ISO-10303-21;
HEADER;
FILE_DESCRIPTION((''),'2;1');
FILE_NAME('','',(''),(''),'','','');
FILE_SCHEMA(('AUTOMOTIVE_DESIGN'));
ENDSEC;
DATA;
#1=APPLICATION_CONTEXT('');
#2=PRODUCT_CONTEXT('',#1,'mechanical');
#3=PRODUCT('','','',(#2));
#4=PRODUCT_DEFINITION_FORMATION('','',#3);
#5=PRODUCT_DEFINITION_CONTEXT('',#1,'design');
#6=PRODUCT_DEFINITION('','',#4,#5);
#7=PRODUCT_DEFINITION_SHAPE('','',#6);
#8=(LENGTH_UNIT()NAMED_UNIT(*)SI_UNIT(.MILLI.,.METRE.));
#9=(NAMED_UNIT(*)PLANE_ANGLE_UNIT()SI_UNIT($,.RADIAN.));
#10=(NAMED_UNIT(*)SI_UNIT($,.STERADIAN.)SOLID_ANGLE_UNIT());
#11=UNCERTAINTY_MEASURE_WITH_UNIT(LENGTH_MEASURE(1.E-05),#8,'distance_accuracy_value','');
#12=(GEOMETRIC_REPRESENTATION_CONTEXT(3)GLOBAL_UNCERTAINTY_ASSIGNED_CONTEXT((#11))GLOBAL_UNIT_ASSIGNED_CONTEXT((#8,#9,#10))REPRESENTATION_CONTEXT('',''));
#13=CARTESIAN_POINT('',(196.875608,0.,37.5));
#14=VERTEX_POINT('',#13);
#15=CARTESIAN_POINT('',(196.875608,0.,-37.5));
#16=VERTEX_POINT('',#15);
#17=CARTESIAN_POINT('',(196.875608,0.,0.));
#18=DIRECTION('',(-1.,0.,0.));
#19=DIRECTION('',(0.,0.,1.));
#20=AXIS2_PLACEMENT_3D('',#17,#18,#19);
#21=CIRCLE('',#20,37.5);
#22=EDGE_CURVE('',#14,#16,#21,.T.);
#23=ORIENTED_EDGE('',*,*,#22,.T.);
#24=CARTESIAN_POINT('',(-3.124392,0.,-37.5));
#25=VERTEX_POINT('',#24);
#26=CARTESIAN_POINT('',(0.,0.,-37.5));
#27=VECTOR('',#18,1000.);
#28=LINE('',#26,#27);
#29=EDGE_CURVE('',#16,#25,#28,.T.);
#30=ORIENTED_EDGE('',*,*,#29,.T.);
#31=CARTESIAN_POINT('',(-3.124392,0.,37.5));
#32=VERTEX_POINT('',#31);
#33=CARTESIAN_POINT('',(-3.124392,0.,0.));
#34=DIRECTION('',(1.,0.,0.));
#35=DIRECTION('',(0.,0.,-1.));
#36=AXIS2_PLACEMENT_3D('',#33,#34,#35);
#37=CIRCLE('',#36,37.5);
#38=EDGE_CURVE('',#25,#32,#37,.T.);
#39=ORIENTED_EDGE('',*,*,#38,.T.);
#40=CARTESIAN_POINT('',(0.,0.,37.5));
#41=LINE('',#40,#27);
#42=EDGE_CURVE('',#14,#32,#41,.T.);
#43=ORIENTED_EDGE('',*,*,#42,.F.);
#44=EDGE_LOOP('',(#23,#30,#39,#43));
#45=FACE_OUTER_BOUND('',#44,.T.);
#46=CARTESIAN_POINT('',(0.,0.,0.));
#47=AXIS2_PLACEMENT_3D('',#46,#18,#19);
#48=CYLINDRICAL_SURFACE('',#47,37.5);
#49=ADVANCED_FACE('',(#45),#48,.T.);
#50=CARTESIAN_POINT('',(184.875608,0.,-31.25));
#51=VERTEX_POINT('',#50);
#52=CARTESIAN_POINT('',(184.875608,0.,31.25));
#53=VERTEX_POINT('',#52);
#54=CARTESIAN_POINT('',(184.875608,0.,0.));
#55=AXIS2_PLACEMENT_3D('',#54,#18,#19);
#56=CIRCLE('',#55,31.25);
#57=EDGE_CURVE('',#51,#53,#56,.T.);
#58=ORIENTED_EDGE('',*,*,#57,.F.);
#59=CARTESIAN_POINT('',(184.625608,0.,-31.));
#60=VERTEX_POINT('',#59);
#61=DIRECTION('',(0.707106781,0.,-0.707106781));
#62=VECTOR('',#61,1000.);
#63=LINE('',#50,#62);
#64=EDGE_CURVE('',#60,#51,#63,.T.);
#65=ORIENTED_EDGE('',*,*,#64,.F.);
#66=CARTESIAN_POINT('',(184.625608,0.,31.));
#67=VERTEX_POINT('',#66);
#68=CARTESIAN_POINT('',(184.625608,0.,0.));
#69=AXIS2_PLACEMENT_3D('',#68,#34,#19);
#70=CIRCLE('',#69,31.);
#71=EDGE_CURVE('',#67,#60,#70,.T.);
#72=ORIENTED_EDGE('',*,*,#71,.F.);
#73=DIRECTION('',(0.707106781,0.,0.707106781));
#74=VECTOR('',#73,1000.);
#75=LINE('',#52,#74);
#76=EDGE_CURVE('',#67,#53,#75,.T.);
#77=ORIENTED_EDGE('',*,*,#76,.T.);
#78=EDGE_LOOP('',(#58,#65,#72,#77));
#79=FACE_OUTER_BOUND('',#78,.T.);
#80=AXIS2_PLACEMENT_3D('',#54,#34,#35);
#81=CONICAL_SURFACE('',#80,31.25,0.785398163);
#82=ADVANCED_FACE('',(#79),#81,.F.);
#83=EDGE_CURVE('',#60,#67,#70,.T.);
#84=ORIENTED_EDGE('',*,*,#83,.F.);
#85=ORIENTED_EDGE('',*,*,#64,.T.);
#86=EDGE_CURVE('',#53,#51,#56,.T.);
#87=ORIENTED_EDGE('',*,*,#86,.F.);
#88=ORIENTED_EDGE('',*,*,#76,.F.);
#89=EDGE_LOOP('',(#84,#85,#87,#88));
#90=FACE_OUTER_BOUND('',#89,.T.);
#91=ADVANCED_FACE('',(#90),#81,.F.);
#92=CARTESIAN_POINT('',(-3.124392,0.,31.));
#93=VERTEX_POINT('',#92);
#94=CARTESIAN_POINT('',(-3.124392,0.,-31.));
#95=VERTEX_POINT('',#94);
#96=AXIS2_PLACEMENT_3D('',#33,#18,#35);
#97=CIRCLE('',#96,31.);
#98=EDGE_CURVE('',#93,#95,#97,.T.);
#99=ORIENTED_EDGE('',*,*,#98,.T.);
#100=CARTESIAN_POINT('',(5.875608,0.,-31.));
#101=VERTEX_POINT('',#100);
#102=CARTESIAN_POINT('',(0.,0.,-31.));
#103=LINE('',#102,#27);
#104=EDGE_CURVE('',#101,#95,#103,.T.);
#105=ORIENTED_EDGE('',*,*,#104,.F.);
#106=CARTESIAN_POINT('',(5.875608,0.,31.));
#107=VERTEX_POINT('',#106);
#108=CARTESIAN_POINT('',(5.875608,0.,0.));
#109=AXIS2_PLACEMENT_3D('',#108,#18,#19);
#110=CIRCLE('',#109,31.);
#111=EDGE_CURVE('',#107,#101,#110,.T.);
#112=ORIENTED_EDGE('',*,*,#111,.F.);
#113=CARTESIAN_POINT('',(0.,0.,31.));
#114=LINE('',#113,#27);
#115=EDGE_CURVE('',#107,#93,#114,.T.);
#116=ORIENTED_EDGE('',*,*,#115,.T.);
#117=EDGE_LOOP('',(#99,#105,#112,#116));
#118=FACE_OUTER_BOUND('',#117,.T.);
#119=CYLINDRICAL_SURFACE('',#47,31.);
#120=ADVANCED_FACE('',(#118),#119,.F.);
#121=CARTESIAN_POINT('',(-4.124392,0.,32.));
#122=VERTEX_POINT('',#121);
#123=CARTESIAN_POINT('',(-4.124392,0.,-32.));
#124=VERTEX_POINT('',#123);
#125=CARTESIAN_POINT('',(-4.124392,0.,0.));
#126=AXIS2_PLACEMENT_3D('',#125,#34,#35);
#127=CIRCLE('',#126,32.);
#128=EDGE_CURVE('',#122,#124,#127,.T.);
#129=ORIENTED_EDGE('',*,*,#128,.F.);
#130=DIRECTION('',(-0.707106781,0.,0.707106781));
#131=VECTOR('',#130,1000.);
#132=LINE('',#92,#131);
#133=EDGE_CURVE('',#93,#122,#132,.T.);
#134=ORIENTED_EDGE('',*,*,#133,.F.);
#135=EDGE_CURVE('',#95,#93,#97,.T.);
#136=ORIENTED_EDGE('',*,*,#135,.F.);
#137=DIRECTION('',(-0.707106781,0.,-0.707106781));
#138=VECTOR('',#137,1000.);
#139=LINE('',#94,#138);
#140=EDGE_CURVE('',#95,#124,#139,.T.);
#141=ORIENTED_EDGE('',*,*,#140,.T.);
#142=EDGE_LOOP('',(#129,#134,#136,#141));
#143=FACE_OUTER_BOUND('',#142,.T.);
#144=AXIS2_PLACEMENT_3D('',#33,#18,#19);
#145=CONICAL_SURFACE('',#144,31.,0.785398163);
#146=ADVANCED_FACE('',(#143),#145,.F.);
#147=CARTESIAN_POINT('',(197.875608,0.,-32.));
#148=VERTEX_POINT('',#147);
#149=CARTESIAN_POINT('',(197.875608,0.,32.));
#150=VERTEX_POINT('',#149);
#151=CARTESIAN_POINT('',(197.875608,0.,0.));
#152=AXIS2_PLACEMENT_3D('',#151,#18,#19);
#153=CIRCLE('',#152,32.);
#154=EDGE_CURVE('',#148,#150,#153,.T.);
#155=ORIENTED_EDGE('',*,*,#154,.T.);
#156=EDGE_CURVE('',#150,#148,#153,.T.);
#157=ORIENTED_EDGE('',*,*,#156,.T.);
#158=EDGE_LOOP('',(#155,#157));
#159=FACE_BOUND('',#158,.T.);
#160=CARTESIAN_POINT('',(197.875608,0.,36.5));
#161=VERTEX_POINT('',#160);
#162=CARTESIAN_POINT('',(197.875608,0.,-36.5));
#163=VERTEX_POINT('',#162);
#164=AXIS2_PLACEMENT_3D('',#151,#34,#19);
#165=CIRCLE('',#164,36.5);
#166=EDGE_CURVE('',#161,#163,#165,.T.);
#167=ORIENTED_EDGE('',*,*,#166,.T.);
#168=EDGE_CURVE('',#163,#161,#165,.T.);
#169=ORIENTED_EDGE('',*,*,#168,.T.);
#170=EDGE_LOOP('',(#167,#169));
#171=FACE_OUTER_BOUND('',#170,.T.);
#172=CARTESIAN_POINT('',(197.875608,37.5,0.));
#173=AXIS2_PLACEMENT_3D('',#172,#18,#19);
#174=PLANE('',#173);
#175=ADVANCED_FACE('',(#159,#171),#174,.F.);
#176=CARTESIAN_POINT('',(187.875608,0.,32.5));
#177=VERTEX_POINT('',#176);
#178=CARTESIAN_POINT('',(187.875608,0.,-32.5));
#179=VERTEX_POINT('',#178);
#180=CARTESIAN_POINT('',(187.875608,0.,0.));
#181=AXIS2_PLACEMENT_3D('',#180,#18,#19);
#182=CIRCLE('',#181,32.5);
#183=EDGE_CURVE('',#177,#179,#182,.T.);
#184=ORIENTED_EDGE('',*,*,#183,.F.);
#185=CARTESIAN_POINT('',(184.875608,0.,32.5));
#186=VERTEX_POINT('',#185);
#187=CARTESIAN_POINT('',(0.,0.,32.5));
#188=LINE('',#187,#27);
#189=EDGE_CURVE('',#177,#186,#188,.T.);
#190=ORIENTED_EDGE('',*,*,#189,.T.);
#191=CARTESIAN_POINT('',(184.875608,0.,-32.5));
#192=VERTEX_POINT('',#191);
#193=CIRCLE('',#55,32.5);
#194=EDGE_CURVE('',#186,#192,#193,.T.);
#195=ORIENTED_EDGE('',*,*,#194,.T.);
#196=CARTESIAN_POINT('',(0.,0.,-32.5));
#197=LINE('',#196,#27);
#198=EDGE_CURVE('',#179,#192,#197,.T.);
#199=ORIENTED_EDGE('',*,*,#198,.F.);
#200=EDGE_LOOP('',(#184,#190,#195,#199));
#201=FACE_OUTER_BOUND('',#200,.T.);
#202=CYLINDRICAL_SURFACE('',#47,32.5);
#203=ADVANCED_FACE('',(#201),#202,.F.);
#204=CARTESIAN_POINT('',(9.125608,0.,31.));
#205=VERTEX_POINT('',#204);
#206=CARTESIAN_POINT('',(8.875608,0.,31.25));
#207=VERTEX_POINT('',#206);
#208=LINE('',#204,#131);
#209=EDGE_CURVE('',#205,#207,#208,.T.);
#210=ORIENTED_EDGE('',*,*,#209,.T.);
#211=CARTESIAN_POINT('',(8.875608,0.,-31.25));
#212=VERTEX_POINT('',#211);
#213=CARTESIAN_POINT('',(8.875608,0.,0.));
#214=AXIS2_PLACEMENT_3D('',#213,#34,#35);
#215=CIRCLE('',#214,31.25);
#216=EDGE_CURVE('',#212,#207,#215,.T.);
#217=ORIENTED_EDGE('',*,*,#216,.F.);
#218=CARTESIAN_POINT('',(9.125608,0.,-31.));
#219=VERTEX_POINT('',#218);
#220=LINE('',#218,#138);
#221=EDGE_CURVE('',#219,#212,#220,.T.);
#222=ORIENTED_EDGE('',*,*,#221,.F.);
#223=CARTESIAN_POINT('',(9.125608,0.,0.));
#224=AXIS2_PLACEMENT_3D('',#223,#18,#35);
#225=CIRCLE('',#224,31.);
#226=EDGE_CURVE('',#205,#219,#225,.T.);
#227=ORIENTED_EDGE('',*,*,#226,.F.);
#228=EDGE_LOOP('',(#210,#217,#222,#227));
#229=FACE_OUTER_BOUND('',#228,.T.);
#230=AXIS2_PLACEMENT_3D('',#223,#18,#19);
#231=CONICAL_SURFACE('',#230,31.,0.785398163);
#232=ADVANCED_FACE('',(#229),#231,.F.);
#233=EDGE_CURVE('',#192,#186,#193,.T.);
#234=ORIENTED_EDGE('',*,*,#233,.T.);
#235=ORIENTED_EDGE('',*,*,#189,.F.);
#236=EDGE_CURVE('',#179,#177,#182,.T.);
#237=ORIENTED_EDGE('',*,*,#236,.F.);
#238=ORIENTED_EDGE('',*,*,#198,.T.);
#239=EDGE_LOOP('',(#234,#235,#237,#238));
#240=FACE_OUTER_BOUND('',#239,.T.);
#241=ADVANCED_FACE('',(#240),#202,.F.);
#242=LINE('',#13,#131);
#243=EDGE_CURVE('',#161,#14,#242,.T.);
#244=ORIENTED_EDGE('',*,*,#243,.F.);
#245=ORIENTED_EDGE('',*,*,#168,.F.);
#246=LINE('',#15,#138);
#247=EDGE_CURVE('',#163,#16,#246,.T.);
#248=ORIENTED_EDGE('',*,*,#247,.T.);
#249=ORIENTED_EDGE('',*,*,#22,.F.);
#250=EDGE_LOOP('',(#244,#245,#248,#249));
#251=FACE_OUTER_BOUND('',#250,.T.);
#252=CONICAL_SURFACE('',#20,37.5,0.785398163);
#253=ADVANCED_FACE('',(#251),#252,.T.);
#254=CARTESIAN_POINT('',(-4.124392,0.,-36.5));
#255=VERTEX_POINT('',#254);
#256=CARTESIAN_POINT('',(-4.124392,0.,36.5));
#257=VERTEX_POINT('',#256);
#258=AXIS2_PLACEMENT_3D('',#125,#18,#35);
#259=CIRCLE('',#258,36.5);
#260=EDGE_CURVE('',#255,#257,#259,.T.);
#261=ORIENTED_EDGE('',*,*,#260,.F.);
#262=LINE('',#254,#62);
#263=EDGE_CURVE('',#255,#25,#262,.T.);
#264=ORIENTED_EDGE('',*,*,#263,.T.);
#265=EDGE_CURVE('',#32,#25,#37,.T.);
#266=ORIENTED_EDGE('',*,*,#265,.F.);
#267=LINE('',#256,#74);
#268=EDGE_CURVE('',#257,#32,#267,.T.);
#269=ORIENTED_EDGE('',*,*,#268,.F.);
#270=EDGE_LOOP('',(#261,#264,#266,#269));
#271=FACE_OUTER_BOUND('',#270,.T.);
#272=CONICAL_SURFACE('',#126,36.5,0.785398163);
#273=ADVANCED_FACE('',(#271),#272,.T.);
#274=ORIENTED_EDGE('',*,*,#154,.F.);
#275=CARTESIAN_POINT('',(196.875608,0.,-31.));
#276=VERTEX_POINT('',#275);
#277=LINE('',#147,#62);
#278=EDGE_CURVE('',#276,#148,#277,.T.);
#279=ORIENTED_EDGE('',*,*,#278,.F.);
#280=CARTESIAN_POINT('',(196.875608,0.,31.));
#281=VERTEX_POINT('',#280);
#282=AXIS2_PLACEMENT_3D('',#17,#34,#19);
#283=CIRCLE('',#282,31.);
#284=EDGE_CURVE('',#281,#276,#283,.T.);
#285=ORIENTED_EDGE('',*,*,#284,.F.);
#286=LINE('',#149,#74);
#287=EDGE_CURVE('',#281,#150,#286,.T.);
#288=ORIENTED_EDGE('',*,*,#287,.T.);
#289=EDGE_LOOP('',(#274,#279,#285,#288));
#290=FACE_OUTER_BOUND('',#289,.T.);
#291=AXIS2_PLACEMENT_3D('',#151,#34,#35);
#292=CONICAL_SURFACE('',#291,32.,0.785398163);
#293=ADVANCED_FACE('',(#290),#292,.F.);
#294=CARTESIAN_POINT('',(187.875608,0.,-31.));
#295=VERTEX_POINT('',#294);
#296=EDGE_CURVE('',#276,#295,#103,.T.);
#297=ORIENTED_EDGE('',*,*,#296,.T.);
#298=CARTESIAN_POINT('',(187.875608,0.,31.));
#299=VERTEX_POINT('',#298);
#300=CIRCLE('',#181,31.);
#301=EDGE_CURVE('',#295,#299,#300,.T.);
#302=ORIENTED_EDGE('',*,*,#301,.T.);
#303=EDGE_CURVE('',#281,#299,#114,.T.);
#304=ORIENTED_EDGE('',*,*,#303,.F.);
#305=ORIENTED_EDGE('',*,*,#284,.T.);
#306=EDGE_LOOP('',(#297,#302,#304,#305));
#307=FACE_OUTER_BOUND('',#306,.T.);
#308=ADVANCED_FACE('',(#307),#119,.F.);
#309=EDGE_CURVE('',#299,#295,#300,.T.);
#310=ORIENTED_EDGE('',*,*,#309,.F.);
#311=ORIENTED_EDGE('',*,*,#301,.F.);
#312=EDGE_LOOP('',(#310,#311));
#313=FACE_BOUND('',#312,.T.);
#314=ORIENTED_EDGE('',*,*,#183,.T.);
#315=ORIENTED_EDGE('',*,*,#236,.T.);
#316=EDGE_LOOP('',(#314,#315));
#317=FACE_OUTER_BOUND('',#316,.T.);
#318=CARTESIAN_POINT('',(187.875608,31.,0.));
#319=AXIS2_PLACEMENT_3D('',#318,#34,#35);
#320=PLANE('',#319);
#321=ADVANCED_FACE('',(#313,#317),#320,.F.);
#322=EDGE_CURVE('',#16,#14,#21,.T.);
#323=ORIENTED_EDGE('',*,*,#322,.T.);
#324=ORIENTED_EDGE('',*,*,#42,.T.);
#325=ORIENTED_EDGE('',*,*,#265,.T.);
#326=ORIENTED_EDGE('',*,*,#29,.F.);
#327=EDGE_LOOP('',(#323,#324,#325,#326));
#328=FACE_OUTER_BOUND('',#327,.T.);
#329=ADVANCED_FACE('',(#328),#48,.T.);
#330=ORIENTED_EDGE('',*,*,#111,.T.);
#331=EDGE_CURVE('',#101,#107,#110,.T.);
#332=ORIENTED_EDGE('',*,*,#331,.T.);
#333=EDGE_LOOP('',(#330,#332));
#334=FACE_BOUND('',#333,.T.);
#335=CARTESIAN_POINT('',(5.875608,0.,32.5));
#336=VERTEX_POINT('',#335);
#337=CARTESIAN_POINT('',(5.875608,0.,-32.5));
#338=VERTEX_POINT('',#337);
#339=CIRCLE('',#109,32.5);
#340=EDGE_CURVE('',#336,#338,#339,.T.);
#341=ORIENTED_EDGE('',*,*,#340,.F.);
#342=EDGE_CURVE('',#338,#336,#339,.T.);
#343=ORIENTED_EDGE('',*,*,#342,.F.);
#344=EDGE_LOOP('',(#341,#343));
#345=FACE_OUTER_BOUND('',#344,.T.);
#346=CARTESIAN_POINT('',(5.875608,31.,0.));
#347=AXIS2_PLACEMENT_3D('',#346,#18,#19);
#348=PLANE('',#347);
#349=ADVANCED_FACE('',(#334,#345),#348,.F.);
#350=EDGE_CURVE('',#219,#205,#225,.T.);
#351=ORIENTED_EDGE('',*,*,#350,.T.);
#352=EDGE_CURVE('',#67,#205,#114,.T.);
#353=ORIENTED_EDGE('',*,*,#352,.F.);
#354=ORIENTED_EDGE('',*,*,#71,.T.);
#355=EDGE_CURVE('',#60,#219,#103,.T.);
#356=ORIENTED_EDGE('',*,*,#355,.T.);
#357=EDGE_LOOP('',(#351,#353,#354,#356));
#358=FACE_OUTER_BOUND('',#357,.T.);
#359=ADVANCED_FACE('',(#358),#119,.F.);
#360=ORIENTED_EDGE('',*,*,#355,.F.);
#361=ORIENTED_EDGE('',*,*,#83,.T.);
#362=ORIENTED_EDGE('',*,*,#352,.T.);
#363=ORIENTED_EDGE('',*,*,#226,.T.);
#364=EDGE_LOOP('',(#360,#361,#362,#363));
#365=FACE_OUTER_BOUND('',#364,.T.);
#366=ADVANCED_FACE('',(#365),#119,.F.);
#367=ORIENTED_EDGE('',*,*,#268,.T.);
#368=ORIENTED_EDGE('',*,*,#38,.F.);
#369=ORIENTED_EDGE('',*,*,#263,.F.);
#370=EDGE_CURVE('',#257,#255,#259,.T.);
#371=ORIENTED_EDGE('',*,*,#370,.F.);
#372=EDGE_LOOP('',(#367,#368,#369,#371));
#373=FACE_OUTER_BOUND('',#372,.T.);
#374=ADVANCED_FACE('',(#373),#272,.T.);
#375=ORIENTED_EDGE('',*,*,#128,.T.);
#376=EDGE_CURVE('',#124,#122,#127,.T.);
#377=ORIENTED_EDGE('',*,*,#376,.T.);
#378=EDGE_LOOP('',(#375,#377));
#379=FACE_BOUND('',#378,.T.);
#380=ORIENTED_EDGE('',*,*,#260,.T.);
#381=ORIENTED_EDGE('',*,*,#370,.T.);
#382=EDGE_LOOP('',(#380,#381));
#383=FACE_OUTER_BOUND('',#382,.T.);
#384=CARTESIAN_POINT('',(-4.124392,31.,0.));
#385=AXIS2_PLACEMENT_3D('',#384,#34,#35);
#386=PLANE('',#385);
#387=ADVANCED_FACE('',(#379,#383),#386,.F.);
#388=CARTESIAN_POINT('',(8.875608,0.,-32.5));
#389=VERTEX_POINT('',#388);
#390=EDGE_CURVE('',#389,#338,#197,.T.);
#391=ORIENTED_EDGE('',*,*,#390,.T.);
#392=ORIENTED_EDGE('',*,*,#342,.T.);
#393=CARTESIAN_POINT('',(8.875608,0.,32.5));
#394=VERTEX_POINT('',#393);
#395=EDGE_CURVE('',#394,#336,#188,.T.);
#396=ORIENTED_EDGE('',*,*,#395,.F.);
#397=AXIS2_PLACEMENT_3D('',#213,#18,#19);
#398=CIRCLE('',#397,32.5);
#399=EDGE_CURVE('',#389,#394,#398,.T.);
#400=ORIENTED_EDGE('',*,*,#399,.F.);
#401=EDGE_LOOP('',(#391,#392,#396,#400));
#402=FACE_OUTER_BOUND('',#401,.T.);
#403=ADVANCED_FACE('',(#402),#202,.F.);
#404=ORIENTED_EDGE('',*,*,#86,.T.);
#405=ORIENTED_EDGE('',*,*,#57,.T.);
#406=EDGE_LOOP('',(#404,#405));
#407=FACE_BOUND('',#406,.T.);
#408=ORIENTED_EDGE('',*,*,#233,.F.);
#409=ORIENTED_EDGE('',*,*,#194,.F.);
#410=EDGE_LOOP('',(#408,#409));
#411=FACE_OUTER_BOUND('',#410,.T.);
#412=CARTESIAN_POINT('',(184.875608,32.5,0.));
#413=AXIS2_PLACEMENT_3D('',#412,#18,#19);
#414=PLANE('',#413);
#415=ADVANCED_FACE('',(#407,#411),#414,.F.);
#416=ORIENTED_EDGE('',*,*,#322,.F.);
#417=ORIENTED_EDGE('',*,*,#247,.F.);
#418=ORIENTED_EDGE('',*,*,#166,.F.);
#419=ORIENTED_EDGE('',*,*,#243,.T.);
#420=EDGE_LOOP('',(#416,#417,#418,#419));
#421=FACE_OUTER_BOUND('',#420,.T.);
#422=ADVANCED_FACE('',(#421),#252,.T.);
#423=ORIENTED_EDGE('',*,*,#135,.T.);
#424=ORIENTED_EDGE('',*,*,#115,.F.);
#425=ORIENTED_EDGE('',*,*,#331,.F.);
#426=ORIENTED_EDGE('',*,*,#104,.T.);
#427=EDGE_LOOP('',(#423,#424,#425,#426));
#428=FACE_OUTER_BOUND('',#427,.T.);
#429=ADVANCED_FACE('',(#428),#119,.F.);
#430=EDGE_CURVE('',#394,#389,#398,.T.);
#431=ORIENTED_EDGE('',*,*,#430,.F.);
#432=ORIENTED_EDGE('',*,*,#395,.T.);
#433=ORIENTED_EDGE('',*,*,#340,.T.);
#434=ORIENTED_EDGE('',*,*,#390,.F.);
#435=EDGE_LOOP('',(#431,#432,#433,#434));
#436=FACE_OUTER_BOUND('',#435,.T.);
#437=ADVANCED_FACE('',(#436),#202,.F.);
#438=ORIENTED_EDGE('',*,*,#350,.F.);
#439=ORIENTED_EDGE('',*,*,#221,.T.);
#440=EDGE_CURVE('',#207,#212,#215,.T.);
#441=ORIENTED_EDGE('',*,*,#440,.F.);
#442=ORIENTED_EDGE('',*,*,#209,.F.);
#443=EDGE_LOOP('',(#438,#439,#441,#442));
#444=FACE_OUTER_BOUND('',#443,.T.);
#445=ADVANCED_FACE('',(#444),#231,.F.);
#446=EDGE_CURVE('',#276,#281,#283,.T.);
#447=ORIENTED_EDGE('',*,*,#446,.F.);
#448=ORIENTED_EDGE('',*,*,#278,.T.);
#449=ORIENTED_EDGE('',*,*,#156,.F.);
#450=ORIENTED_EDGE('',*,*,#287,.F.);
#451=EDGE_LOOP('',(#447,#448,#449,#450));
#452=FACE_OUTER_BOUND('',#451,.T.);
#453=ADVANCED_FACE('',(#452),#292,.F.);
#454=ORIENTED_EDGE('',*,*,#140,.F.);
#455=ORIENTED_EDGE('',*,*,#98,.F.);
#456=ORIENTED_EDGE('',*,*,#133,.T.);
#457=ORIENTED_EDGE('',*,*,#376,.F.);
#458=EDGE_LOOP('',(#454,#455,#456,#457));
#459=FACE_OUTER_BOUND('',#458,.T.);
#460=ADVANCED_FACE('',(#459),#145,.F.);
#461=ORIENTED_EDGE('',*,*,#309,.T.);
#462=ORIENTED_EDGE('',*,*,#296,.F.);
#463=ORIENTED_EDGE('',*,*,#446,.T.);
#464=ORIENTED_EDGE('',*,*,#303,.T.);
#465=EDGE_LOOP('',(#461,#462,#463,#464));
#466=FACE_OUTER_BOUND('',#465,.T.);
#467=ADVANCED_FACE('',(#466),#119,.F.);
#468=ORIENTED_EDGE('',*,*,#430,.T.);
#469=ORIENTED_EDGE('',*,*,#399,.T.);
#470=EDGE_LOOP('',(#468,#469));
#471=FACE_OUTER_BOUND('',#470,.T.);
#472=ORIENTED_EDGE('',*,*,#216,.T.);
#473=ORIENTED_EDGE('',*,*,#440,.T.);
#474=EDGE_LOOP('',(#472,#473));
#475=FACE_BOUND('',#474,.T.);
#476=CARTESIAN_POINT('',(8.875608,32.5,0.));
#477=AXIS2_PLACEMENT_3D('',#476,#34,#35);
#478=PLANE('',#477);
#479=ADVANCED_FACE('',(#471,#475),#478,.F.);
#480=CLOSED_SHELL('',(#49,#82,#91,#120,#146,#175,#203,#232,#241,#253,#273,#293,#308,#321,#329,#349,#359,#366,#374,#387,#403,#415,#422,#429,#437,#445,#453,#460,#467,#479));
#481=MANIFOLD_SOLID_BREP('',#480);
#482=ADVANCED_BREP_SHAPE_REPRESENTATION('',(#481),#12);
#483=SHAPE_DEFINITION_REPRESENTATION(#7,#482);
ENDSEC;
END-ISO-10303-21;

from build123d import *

# Parameters (mm, degrees)
CHAMFER_1_SIZE = 1
CHAMFER_2_SIZE = 0.25


with BuildPart() as part:
    # 草图1 → 旋转1 (revolve)
    with BuildSketch(Plane.XY, mode=Mode.PRIVATE) as revolve_1_sk:
        Polygon((-4.124391585, 31), (5.875608415, 31), (5.875608415, 32.5), (8.875608415, 32.5), (8.875608415, 31), (184.875608415, 31), (184.875608415, 32.5), (187.875608415, 32.5), (187.875608415, 31), (197.875608415, 31), (197.875608415, 37.5), (-4.124391585, 37.5), align=None)
    revolve(revolve_1_sk.sketch.rotate(Axis((0, 0, 0), (1, 0, 0)), 90), axis=Axis((0, 0, 0), (1, 0, 0)))

    # 倒角1
    chamfer_1_edges = [part.edges().sort_by_distance(p)[0] for p in [
        (197.875608415, 0, -31),
        (197.875608415, 0, -37.5),
        (-4.124391585, 0, -37.5),
        (-4.124391585, 0, -31),
    ]]
    chamfer(chamfer_1_edges, length=CHAMFER_1_SIZE)

    # 倒角2
    chamfer_2_edges = [part.edges().sort_by_distance(p)[0] for p in [
        (8.875608415, 0, -31),
        (184.875608415, 0, -31),
    ]]
    chamfer(chamfer_2_edges, length=CHAMFER_2_SIZE)


solid = part.part
